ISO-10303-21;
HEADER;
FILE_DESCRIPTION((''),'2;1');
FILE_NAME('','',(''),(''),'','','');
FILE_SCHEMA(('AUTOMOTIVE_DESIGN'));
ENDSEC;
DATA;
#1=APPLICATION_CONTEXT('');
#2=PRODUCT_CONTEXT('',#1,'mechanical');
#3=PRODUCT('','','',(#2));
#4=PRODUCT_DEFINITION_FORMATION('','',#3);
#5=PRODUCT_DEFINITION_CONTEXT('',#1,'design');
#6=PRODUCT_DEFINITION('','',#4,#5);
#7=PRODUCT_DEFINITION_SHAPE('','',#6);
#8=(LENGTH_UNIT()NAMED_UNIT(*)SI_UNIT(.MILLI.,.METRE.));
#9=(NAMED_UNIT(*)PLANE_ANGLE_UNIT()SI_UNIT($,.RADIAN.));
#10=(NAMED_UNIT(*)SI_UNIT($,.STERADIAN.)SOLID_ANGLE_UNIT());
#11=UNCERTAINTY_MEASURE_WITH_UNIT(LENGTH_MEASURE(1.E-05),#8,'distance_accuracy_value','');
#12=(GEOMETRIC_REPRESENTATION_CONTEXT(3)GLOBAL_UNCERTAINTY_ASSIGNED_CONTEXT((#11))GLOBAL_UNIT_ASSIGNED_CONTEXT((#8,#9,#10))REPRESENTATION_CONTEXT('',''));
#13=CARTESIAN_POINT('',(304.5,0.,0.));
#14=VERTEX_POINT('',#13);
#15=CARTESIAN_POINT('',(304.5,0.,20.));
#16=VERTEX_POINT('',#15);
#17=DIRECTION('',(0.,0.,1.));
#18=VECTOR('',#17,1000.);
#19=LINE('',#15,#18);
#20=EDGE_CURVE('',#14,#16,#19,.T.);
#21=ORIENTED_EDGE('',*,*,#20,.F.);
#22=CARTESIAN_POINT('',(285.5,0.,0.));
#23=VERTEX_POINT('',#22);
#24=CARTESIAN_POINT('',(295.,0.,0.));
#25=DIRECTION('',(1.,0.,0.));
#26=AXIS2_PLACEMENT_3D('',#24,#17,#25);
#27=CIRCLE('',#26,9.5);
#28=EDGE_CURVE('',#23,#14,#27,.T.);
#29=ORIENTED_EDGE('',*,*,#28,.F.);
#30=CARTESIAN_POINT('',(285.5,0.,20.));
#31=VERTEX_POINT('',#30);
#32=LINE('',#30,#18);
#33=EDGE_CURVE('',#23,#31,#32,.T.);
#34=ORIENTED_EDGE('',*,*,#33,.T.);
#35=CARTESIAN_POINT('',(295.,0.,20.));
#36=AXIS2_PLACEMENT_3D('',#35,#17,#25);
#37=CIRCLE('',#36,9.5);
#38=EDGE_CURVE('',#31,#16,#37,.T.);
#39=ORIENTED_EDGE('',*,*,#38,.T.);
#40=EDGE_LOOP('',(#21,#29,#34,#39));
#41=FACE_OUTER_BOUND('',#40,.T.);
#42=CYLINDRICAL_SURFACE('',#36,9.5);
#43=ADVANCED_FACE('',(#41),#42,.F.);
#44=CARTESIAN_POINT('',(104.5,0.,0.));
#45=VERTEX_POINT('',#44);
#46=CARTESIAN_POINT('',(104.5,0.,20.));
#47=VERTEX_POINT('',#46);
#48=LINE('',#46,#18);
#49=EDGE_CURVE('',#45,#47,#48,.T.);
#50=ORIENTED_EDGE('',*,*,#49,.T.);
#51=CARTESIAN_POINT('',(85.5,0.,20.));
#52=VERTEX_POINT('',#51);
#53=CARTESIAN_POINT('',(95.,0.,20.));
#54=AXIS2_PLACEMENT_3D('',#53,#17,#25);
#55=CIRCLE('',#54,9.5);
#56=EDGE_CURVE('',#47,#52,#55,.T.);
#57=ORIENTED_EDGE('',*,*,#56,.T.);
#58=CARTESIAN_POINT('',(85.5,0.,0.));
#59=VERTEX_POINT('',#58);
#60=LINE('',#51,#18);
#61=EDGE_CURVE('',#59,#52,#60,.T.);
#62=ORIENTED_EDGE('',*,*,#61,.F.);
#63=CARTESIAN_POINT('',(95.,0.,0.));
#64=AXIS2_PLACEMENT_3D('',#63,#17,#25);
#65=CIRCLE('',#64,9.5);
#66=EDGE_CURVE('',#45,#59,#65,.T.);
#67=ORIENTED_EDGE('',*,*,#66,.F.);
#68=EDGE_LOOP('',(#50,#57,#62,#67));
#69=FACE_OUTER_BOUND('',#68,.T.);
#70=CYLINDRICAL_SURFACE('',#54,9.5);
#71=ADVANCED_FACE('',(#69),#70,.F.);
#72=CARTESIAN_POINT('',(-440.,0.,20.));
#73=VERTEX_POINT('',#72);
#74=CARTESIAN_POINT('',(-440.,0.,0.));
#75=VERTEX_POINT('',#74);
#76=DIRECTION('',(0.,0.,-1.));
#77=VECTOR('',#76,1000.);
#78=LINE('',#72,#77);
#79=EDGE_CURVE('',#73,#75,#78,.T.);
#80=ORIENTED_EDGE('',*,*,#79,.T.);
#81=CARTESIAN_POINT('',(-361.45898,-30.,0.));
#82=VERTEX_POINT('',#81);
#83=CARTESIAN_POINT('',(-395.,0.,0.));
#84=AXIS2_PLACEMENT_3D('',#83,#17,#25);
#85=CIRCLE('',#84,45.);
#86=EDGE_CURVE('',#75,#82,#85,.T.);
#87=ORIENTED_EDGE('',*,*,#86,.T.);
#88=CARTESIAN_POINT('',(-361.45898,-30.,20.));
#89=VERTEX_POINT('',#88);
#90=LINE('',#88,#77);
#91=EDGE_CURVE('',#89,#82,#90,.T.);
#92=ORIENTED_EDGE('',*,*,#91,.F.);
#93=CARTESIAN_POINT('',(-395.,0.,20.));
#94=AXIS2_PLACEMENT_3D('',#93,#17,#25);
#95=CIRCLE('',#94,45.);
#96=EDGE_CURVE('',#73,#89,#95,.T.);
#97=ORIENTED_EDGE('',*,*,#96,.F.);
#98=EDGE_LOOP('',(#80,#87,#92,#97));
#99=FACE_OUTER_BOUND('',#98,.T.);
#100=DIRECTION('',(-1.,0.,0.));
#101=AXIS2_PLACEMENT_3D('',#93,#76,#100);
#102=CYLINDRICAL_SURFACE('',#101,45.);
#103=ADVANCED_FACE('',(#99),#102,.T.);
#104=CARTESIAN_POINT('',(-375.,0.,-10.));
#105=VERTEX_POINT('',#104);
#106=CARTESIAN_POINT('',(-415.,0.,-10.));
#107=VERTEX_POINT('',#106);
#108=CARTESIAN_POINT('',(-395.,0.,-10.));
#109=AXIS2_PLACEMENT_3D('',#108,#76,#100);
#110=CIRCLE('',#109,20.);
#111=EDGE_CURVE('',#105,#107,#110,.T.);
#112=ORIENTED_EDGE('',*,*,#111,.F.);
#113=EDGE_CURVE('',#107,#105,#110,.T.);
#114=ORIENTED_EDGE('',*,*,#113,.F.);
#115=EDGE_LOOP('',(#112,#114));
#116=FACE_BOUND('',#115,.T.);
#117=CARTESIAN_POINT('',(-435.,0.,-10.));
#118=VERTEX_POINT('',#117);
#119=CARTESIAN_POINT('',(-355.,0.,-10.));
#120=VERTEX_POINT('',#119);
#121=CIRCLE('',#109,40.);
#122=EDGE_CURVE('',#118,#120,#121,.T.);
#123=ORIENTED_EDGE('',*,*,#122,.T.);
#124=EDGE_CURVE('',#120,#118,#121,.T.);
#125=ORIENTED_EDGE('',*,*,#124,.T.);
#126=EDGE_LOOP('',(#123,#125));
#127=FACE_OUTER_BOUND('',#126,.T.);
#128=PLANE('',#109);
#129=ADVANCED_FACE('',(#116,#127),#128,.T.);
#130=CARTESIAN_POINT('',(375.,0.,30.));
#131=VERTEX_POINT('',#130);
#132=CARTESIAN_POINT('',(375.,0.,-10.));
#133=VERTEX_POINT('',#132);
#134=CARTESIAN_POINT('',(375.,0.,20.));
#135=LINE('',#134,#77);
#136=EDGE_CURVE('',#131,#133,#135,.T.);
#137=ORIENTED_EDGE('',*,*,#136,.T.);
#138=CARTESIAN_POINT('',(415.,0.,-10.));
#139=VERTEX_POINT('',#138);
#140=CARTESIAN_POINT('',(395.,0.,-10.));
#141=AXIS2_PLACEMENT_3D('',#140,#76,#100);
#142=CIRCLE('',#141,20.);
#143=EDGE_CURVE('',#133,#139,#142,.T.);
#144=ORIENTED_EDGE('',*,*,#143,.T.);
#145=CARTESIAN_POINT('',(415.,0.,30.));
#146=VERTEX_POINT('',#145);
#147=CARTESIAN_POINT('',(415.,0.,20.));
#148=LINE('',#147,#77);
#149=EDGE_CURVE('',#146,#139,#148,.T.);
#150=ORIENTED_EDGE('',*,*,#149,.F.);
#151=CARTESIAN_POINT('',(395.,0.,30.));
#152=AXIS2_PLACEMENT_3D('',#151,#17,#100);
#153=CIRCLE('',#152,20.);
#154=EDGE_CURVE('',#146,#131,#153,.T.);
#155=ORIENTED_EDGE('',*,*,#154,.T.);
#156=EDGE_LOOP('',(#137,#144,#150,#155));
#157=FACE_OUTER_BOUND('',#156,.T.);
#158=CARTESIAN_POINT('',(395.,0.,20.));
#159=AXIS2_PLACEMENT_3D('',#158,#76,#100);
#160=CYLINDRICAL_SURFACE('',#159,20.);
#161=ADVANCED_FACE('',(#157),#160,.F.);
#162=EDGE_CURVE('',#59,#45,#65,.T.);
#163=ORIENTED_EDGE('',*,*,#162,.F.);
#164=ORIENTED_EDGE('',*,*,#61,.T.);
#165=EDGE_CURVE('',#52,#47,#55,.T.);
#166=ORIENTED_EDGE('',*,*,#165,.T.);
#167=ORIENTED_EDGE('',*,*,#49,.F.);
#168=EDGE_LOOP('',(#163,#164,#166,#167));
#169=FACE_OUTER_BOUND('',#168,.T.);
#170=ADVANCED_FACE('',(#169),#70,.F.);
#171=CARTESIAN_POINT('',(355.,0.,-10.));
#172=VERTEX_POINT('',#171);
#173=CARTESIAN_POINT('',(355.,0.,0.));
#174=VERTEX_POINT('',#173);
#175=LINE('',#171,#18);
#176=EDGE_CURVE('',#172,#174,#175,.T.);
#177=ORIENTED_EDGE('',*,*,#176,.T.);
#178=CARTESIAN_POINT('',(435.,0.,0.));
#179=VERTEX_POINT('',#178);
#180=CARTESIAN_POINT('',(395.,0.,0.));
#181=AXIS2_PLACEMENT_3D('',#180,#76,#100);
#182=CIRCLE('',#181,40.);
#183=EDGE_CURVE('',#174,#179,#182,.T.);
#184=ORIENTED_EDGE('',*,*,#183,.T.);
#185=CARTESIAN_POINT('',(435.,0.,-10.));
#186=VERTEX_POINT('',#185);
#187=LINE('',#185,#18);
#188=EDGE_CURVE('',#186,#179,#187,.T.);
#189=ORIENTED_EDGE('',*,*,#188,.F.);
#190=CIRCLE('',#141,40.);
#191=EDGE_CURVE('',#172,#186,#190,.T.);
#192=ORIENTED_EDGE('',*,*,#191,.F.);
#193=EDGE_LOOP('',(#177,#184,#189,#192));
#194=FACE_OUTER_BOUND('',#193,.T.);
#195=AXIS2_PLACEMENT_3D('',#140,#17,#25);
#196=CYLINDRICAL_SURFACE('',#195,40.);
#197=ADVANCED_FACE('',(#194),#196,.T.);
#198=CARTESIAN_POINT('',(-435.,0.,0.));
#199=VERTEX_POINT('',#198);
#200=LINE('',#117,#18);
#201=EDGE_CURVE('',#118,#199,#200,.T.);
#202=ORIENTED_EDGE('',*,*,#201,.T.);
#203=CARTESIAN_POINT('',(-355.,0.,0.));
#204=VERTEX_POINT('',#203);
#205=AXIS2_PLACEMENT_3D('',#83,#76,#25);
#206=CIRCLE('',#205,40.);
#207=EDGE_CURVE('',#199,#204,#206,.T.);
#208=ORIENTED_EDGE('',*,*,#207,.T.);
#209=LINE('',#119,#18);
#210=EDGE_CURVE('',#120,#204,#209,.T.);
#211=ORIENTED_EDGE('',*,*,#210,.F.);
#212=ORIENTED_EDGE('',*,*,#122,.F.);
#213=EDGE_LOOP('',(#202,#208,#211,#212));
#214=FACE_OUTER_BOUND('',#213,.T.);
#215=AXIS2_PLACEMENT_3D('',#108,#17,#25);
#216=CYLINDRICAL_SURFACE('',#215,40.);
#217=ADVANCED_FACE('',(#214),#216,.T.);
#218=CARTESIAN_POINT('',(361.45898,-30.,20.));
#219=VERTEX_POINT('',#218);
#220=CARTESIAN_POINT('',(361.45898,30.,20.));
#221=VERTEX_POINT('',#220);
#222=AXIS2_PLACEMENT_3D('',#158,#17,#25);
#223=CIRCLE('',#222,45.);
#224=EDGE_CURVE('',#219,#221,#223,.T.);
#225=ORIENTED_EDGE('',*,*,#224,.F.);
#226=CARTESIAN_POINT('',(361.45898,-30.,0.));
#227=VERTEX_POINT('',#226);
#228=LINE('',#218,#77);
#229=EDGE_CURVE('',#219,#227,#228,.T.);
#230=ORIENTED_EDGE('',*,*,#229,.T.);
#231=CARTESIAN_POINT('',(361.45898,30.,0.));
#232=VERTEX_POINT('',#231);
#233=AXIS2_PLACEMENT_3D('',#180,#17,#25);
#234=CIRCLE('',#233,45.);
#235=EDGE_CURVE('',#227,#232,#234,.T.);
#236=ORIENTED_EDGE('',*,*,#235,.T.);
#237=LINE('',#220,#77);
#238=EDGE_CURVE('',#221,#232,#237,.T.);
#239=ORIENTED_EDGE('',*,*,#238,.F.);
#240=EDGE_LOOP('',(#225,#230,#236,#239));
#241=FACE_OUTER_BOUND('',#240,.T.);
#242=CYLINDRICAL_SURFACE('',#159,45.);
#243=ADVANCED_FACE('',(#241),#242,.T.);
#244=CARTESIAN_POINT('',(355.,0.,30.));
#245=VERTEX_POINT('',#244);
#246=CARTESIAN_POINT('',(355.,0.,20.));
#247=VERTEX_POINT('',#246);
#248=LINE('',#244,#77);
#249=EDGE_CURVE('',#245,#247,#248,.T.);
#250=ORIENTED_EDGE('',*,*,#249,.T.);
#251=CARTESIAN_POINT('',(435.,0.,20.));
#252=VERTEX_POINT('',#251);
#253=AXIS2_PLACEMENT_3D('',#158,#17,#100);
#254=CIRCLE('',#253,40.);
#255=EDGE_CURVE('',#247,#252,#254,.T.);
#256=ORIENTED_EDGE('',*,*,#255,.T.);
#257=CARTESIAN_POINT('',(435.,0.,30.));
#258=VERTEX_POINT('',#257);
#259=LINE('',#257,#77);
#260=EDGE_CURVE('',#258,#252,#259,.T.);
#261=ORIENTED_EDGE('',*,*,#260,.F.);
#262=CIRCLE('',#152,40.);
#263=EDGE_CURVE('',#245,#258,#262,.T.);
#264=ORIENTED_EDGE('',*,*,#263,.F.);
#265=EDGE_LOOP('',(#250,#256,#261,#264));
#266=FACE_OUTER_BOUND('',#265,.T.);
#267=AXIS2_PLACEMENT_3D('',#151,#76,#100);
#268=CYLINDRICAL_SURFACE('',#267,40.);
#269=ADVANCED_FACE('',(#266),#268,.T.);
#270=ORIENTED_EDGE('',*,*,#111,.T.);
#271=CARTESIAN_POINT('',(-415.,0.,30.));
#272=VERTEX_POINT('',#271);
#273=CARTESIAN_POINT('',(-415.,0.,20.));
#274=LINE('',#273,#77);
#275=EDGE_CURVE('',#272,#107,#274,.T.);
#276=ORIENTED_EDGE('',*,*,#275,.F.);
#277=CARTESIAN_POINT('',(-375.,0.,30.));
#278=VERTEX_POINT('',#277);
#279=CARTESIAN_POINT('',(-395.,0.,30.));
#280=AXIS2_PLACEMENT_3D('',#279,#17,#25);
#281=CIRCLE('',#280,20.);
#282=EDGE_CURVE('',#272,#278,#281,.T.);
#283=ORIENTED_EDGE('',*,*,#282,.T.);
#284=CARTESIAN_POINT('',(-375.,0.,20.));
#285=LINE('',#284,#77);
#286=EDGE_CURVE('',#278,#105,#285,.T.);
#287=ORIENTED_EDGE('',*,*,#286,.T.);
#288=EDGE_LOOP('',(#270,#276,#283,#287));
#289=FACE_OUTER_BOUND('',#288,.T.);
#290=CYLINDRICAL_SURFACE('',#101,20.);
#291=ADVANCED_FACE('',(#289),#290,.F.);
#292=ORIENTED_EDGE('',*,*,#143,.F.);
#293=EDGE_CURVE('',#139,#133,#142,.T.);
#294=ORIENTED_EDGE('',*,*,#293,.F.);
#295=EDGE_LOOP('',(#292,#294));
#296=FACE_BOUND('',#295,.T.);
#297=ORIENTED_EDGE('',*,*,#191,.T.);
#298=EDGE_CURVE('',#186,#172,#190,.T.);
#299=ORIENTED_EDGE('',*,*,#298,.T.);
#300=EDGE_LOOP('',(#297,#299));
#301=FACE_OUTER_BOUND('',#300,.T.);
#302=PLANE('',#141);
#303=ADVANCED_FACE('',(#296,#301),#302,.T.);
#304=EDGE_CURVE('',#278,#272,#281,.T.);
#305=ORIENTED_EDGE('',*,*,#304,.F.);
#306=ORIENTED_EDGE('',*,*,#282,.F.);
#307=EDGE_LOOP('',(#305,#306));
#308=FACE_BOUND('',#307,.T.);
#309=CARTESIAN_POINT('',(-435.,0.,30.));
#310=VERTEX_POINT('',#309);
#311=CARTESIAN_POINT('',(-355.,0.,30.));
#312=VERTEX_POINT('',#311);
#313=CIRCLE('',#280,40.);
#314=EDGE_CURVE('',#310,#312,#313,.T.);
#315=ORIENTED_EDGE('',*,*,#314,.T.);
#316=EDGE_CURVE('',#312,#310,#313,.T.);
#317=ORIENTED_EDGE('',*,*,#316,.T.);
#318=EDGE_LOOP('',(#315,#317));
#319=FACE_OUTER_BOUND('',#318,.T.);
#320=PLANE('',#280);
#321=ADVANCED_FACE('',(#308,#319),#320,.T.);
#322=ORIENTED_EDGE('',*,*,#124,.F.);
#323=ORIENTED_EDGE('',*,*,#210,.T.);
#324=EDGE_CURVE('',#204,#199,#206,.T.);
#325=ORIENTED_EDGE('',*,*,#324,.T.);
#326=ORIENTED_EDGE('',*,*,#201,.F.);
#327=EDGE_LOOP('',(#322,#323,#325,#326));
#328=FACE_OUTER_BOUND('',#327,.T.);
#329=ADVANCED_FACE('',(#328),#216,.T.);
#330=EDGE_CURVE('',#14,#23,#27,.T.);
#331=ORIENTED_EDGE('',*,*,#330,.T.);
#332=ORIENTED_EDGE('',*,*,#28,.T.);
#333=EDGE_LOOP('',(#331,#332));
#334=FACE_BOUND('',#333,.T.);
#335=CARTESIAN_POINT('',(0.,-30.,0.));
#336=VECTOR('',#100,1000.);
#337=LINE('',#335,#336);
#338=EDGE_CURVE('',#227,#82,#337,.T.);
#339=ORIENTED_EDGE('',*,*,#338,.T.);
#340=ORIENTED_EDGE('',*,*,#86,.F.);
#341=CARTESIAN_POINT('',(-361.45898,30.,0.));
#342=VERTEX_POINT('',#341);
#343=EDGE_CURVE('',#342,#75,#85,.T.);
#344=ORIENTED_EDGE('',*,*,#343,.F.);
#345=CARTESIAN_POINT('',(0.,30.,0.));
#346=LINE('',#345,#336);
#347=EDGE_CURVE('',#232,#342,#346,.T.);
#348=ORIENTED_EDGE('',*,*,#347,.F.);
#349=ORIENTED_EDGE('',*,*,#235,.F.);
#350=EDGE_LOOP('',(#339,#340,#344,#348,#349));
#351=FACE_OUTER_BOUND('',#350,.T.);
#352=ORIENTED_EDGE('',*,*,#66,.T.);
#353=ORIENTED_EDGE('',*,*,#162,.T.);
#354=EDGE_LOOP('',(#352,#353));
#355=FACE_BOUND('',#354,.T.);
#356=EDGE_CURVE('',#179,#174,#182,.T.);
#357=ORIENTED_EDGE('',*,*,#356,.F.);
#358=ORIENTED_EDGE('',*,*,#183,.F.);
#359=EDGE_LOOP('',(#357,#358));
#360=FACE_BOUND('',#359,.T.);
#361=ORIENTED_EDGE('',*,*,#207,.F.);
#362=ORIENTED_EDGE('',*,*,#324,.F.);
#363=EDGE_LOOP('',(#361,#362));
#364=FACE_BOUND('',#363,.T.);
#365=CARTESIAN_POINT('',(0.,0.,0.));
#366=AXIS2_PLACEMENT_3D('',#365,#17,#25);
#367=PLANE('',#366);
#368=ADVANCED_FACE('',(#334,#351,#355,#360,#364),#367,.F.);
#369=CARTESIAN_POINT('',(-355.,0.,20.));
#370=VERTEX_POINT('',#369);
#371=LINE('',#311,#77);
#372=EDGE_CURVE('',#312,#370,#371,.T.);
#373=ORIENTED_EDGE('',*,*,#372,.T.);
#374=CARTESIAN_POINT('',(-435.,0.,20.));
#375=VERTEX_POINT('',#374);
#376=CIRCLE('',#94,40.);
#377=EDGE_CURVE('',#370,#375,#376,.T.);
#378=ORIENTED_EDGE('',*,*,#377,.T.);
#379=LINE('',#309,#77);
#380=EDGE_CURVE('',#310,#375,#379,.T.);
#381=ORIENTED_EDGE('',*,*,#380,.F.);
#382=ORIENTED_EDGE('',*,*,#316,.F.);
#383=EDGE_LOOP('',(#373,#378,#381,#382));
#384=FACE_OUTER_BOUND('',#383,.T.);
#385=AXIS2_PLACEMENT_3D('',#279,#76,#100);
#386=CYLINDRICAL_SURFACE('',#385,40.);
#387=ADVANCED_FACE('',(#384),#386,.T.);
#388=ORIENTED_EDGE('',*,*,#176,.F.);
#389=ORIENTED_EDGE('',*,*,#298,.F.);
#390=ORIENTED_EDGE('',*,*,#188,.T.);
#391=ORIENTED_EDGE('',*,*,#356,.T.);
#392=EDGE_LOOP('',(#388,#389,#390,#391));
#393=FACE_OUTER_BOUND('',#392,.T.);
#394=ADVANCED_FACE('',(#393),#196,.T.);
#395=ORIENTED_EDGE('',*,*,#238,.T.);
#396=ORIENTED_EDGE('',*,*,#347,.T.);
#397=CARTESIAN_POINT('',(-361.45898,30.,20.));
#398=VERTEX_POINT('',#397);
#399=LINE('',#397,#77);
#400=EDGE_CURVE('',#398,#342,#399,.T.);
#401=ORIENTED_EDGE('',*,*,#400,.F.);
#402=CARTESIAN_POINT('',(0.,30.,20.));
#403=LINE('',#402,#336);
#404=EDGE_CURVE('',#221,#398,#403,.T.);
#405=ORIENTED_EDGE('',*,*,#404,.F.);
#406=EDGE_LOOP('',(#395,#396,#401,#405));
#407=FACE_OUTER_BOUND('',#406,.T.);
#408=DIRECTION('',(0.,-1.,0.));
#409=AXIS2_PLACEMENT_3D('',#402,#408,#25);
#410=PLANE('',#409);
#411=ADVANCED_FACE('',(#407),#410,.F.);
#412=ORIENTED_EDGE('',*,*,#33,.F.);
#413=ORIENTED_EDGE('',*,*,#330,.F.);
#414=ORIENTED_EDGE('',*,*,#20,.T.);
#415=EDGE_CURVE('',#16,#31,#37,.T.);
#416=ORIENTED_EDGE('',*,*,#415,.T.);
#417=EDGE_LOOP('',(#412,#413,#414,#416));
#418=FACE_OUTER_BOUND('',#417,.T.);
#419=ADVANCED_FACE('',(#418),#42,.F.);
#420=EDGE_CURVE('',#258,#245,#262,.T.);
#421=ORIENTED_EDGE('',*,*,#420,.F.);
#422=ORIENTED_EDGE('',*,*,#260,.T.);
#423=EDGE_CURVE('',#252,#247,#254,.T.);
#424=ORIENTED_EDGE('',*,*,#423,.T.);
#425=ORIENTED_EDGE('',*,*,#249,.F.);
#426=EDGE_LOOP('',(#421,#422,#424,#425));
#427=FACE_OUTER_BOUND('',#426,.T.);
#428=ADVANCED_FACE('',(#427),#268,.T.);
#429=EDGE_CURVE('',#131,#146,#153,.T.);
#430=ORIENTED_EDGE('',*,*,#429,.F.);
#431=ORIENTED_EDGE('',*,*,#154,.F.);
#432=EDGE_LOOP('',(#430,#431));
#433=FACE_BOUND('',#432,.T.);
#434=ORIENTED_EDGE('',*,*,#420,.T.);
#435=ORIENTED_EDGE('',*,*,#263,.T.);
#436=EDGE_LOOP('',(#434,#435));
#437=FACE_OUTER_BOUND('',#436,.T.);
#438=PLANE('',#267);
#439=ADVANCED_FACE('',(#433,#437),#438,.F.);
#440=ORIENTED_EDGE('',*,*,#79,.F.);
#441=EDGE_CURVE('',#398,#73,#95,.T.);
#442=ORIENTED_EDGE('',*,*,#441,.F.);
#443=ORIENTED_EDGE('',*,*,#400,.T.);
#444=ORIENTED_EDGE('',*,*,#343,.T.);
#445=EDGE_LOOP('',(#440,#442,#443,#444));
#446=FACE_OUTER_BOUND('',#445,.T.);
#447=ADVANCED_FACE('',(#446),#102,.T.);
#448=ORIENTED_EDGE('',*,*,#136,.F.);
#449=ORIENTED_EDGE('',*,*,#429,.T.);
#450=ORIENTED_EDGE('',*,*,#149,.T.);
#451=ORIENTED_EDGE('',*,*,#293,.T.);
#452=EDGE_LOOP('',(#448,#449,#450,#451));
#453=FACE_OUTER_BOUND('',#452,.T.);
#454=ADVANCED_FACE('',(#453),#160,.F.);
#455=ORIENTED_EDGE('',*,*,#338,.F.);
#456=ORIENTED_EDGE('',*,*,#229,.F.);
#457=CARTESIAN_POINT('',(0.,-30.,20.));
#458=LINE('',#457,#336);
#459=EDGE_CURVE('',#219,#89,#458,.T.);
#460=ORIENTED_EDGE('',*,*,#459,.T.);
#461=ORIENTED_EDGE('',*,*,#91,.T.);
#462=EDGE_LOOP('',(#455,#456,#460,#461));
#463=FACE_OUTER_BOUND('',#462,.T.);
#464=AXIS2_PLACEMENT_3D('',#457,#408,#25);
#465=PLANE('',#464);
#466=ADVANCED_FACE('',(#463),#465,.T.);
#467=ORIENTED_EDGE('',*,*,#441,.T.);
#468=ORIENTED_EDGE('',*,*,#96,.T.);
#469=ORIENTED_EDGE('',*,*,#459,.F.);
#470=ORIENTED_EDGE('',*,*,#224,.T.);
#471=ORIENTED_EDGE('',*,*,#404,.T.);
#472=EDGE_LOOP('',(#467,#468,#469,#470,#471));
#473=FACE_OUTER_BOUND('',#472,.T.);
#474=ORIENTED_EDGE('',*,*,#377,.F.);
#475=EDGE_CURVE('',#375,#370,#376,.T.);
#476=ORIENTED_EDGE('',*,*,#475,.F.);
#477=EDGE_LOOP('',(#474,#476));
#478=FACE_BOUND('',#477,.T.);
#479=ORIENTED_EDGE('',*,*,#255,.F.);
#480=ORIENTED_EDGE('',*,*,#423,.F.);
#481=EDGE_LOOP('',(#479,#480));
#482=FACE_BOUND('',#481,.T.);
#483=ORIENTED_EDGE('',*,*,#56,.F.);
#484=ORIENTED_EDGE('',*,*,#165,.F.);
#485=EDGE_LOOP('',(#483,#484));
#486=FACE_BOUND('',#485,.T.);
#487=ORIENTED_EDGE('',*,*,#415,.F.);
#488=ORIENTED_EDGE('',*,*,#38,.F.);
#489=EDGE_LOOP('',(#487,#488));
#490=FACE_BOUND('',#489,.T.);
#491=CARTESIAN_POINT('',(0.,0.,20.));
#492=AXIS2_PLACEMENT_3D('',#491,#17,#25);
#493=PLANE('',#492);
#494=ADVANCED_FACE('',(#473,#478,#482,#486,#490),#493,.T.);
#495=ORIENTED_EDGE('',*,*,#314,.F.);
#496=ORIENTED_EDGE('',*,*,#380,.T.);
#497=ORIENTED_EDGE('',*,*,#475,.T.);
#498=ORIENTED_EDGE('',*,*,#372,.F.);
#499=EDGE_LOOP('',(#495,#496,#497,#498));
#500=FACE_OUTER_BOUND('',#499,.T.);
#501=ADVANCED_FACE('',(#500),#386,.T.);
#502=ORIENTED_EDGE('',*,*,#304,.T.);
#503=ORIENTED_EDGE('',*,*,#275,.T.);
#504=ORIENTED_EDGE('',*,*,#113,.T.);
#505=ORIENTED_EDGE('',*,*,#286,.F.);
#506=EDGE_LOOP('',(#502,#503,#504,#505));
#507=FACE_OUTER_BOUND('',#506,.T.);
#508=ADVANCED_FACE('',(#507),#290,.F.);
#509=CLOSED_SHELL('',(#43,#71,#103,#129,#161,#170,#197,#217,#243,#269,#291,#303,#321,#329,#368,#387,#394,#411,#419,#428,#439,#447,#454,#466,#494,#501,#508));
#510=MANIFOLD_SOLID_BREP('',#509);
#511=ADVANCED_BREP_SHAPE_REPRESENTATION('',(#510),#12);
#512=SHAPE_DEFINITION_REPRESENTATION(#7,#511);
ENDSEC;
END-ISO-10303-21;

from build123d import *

# Parameters (mm, degrees)
SKETCH_1_R          = 20
EXTRUDE_1_DEPTH     = 20
SKETCH_2_R          = 40
SKETCH_2_R_2        = 20
EXTRUDE_2_DEPTH     = 10
EXTRUDE_START       = 10
SKETCH_3_R          = 40
SKETCH_3_R_2        = 20
EXTRUDE_3_DEPTH     = 10
HOLE_WIZARD_M16_1_D = 19


with BuildPart() as part:
    # 草图1 → 凸台-拉伸1 (new body)
    with BuildSketch(Plane.XY):
        with BuildLine():
            ThreePointArc((361.458980338, -30), (440, 0), (361.458980338, 30))
            Line((361.458980338, 30), (-361.458980338, 30))
            ThreePointArc((-361.458980338, 30), (-440, 0), (-361.458980338, -30))
            Line((-361.458980338, -30), (361.458980338, -30))
        make_face()
        with Locations((395, 0)):
            Circle(SKETCH_1_R, mode=Mode.SUBTRACT)
        with Locations((-395, 0)):
            Circle(SKETCH_1_R, mode=Mode.SUBTRACT)
    extrude(amount=EXTRUDE_1_DEPTH)

    # 草图2 → 凸台-拉伸2 (add)
    # profile 1 of 2: a face of its own
    with BuildSketch(Plane.XY.offset(20)):
        with Locations((-395, 0)):
            Circle(SKETCH_2_R)
        with Locations((-395, 0)):
            Circle(SKETCH_2_R_2, mode=Mode.SUBTRACT)
    # profile 2 of 2: a face of its own
    with BuildSketch(Plane.XY.offset(20)):
        with Locations(Location((395, 0, 0), (0, 0, 180))):
            Circle(SKETCH_2_R)
        with Locations(Location((395, 0, 0), (0, 0, 180))):
            Circle(SKETCH_2_R_2, mode=Mode.SUBTRACT)
    extrude(amount=EXTRUDE_2_DEPTH)

    # 草图3 → 凸台-拉伸3 (add)
    # profile 1 of 2: a face of its own
    with BuildSketch(Plane(origin=(0, 0, 0), x_dir=(-1, 0, 0), z_dir=(0, 0, -1)).offset(EXTRUDE_START)):
        with Locations((-395, 0)):
            Circle(SKETCH_3_R)
        with Locations((-395, 0)):
            Circle(SKETCH_3_R_2, mode=Mode.SUBTRACT)
    # profile 2 of 2: a face of its own
    with BuildSketch(Plane(origin=(0, 0, 0), x_dir=(-1, 0, 0), z_dir=(0, 0, -1)).offset(EXTRUDE_START)):
        with Locations(Location((395, 0, 0), (0, 0, 180))):
            Circle(SKETCH_3_R)
        with Locations((395, 0)):
            Circle(SKETCH_3_R_2, mode=Mode.SUBTRACT)
    extrude(amount=-EXTRUDE_3_DEPTH)

    # M16 间隙孔1 (through all)
    with Locations(Plane.XY.offset(20)):
        with Locations((95, 0), (295, 0)):
            Hole(HOLE_WIZARD_M16_1_D / 2)


solid = part.part
